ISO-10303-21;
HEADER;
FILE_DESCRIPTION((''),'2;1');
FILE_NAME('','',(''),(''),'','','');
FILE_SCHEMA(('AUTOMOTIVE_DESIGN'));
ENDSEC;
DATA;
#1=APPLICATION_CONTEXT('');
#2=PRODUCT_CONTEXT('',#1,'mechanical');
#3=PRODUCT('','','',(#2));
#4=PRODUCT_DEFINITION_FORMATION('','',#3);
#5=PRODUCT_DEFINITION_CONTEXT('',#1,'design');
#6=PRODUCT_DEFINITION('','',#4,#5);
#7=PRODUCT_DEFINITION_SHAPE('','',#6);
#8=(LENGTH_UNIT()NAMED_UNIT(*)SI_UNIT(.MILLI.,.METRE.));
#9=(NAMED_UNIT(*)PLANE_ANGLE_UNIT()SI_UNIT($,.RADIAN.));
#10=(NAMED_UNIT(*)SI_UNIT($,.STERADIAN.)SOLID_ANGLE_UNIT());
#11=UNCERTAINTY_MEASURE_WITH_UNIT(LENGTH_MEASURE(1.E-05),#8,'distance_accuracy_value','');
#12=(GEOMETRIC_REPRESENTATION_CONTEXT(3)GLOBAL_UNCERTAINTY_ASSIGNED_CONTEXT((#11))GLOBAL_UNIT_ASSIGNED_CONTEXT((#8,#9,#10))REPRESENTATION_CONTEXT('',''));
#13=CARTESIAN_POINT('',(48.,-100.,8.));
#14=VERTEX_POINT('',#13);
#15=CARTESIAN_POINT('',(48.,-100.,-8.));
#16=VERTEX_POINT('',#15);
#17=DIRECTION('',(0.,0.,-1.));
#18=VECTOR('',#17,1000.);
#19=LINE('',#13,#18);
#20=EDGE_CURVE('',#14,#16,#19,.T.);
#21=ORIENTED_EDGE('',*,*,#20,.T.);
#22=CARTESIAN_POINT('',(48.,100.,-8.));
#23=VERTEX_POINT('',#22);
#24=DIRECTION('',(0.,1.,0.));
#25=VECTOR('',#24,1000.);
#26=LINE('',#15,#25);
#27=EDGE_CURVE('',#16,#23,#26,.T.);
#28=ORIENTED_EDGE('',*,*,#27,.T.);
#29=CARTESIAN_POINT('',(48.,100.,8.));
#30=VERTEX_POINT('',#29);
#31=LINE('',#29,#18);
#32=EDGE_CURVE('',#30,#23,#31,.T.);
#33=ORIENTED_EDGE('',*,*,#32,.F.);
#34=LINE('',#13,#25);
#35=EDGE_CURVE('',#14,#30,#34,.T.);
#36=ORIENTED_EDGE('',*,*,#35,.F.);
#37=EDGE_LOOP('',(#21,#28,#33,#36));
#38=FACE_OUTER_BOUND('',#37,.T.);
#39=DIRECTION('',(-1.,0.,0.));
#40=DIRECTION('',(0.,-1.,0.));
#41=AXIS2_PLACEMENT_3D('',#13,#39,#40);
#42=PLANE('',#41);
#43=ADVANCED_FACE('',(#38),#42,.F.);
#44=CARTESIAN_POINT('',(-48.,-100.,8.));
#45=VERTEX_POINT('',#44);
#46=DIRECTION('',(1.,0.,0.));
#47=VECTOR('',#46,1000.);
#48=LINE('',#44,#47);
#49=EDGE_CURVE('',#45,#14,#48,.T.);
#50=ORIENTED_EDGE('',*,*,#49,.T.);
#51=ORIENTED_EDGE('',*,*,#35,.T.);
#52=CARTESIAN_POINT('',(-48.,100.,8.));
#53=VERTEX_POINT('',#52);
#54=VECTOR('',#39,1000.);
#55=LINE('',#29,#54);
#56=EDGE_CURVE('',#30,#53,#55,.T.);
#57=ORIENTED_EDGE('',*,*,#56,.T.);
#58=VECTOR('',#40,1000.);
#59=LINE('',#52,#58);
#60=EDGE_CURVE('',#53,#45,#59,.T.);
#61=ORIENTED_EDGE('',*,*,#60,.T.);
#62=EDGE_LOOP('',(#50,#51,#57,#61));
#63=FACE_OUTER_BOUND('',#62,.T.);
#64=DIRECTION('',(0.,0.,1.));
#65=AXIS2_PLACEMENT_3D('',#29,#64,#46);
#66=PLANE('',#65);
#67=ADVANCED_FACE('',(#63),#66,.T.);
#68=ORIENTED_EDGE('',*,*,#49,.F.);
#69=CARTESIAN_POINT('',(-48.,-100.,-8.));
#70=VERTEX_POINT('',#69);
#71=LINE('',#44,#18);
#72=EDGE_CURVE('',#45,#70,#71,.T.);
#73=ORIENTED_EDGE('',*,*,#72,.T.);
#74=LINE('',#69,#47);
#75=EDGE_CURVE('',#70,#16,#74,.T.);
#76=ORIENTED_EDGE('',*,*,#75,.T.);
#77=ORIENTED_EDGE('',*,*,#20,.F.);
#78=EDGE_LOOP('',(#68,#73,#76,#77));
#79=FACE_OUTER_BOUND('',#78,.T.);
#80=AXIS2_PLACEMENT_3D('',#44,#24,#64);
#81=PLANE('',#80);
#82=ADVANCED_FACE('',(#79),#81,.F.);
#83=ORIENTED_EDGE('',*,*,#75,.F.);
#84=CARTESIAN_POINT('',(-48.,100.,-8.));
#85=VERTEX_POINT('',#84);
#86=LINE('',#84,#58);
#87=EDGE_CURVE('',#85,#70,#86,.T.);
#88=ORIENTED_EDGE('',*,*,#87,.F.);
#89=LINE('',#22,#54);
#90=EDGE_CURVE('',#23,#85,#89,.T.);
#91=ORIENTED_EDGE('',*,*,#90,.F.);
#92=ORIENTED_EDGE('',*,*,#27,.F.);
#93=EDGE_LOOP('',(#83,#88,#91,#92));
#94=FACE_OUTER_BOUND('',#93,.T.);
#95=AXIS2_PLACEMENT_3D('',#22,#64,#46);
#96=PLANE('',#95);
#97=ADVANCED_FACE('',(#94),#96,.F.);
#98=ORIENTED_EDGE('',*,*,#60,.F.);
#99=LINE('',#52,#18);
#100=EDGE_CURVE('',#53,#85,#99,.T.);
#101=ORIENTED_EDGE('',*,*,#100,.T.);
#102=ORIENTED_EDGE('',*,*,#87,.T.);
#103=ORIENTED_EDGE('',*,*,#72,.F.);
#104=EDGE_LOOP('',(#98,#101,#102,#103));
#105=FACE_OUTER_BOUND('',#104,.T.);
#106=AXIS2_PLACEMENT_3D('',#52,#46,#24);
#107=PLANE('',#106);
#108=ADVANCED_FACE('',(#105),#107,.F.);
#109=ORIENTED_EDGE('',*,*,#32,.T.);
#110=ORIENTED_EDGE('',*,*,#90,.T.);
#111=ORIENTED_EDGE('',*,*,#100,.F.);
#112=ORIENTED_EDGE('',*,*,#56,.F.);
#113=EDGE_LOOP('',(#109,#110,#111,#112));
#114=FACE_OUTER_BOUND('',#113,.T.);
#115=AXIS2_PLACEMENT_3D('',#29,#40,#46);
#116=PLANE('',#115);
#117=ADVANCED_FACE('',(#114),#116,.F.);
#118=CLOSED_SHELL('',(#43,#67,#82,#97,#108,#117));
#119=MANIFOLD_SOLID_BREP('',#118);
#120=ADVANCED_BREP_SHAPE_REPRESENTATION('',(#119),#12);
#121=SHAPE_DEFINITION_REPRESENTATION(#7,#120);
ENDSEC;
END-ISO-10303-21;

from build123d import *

# Parameters (mm, degrees)
SKETCH1_W      = 96
SKETCH1_H      = 200
EXTRUDE1_DEPTH = 8


with BuildPart() as part:
    # Sketch1 → Extrude1 (new, symmetric)
    with BuildSketch(Plane.XY):
        Rectangle(SKETCH1_W, SKETCH1_H)
    extrude(amount=EXTRUDE1_DEPTH, both=True)


solid = part.part
